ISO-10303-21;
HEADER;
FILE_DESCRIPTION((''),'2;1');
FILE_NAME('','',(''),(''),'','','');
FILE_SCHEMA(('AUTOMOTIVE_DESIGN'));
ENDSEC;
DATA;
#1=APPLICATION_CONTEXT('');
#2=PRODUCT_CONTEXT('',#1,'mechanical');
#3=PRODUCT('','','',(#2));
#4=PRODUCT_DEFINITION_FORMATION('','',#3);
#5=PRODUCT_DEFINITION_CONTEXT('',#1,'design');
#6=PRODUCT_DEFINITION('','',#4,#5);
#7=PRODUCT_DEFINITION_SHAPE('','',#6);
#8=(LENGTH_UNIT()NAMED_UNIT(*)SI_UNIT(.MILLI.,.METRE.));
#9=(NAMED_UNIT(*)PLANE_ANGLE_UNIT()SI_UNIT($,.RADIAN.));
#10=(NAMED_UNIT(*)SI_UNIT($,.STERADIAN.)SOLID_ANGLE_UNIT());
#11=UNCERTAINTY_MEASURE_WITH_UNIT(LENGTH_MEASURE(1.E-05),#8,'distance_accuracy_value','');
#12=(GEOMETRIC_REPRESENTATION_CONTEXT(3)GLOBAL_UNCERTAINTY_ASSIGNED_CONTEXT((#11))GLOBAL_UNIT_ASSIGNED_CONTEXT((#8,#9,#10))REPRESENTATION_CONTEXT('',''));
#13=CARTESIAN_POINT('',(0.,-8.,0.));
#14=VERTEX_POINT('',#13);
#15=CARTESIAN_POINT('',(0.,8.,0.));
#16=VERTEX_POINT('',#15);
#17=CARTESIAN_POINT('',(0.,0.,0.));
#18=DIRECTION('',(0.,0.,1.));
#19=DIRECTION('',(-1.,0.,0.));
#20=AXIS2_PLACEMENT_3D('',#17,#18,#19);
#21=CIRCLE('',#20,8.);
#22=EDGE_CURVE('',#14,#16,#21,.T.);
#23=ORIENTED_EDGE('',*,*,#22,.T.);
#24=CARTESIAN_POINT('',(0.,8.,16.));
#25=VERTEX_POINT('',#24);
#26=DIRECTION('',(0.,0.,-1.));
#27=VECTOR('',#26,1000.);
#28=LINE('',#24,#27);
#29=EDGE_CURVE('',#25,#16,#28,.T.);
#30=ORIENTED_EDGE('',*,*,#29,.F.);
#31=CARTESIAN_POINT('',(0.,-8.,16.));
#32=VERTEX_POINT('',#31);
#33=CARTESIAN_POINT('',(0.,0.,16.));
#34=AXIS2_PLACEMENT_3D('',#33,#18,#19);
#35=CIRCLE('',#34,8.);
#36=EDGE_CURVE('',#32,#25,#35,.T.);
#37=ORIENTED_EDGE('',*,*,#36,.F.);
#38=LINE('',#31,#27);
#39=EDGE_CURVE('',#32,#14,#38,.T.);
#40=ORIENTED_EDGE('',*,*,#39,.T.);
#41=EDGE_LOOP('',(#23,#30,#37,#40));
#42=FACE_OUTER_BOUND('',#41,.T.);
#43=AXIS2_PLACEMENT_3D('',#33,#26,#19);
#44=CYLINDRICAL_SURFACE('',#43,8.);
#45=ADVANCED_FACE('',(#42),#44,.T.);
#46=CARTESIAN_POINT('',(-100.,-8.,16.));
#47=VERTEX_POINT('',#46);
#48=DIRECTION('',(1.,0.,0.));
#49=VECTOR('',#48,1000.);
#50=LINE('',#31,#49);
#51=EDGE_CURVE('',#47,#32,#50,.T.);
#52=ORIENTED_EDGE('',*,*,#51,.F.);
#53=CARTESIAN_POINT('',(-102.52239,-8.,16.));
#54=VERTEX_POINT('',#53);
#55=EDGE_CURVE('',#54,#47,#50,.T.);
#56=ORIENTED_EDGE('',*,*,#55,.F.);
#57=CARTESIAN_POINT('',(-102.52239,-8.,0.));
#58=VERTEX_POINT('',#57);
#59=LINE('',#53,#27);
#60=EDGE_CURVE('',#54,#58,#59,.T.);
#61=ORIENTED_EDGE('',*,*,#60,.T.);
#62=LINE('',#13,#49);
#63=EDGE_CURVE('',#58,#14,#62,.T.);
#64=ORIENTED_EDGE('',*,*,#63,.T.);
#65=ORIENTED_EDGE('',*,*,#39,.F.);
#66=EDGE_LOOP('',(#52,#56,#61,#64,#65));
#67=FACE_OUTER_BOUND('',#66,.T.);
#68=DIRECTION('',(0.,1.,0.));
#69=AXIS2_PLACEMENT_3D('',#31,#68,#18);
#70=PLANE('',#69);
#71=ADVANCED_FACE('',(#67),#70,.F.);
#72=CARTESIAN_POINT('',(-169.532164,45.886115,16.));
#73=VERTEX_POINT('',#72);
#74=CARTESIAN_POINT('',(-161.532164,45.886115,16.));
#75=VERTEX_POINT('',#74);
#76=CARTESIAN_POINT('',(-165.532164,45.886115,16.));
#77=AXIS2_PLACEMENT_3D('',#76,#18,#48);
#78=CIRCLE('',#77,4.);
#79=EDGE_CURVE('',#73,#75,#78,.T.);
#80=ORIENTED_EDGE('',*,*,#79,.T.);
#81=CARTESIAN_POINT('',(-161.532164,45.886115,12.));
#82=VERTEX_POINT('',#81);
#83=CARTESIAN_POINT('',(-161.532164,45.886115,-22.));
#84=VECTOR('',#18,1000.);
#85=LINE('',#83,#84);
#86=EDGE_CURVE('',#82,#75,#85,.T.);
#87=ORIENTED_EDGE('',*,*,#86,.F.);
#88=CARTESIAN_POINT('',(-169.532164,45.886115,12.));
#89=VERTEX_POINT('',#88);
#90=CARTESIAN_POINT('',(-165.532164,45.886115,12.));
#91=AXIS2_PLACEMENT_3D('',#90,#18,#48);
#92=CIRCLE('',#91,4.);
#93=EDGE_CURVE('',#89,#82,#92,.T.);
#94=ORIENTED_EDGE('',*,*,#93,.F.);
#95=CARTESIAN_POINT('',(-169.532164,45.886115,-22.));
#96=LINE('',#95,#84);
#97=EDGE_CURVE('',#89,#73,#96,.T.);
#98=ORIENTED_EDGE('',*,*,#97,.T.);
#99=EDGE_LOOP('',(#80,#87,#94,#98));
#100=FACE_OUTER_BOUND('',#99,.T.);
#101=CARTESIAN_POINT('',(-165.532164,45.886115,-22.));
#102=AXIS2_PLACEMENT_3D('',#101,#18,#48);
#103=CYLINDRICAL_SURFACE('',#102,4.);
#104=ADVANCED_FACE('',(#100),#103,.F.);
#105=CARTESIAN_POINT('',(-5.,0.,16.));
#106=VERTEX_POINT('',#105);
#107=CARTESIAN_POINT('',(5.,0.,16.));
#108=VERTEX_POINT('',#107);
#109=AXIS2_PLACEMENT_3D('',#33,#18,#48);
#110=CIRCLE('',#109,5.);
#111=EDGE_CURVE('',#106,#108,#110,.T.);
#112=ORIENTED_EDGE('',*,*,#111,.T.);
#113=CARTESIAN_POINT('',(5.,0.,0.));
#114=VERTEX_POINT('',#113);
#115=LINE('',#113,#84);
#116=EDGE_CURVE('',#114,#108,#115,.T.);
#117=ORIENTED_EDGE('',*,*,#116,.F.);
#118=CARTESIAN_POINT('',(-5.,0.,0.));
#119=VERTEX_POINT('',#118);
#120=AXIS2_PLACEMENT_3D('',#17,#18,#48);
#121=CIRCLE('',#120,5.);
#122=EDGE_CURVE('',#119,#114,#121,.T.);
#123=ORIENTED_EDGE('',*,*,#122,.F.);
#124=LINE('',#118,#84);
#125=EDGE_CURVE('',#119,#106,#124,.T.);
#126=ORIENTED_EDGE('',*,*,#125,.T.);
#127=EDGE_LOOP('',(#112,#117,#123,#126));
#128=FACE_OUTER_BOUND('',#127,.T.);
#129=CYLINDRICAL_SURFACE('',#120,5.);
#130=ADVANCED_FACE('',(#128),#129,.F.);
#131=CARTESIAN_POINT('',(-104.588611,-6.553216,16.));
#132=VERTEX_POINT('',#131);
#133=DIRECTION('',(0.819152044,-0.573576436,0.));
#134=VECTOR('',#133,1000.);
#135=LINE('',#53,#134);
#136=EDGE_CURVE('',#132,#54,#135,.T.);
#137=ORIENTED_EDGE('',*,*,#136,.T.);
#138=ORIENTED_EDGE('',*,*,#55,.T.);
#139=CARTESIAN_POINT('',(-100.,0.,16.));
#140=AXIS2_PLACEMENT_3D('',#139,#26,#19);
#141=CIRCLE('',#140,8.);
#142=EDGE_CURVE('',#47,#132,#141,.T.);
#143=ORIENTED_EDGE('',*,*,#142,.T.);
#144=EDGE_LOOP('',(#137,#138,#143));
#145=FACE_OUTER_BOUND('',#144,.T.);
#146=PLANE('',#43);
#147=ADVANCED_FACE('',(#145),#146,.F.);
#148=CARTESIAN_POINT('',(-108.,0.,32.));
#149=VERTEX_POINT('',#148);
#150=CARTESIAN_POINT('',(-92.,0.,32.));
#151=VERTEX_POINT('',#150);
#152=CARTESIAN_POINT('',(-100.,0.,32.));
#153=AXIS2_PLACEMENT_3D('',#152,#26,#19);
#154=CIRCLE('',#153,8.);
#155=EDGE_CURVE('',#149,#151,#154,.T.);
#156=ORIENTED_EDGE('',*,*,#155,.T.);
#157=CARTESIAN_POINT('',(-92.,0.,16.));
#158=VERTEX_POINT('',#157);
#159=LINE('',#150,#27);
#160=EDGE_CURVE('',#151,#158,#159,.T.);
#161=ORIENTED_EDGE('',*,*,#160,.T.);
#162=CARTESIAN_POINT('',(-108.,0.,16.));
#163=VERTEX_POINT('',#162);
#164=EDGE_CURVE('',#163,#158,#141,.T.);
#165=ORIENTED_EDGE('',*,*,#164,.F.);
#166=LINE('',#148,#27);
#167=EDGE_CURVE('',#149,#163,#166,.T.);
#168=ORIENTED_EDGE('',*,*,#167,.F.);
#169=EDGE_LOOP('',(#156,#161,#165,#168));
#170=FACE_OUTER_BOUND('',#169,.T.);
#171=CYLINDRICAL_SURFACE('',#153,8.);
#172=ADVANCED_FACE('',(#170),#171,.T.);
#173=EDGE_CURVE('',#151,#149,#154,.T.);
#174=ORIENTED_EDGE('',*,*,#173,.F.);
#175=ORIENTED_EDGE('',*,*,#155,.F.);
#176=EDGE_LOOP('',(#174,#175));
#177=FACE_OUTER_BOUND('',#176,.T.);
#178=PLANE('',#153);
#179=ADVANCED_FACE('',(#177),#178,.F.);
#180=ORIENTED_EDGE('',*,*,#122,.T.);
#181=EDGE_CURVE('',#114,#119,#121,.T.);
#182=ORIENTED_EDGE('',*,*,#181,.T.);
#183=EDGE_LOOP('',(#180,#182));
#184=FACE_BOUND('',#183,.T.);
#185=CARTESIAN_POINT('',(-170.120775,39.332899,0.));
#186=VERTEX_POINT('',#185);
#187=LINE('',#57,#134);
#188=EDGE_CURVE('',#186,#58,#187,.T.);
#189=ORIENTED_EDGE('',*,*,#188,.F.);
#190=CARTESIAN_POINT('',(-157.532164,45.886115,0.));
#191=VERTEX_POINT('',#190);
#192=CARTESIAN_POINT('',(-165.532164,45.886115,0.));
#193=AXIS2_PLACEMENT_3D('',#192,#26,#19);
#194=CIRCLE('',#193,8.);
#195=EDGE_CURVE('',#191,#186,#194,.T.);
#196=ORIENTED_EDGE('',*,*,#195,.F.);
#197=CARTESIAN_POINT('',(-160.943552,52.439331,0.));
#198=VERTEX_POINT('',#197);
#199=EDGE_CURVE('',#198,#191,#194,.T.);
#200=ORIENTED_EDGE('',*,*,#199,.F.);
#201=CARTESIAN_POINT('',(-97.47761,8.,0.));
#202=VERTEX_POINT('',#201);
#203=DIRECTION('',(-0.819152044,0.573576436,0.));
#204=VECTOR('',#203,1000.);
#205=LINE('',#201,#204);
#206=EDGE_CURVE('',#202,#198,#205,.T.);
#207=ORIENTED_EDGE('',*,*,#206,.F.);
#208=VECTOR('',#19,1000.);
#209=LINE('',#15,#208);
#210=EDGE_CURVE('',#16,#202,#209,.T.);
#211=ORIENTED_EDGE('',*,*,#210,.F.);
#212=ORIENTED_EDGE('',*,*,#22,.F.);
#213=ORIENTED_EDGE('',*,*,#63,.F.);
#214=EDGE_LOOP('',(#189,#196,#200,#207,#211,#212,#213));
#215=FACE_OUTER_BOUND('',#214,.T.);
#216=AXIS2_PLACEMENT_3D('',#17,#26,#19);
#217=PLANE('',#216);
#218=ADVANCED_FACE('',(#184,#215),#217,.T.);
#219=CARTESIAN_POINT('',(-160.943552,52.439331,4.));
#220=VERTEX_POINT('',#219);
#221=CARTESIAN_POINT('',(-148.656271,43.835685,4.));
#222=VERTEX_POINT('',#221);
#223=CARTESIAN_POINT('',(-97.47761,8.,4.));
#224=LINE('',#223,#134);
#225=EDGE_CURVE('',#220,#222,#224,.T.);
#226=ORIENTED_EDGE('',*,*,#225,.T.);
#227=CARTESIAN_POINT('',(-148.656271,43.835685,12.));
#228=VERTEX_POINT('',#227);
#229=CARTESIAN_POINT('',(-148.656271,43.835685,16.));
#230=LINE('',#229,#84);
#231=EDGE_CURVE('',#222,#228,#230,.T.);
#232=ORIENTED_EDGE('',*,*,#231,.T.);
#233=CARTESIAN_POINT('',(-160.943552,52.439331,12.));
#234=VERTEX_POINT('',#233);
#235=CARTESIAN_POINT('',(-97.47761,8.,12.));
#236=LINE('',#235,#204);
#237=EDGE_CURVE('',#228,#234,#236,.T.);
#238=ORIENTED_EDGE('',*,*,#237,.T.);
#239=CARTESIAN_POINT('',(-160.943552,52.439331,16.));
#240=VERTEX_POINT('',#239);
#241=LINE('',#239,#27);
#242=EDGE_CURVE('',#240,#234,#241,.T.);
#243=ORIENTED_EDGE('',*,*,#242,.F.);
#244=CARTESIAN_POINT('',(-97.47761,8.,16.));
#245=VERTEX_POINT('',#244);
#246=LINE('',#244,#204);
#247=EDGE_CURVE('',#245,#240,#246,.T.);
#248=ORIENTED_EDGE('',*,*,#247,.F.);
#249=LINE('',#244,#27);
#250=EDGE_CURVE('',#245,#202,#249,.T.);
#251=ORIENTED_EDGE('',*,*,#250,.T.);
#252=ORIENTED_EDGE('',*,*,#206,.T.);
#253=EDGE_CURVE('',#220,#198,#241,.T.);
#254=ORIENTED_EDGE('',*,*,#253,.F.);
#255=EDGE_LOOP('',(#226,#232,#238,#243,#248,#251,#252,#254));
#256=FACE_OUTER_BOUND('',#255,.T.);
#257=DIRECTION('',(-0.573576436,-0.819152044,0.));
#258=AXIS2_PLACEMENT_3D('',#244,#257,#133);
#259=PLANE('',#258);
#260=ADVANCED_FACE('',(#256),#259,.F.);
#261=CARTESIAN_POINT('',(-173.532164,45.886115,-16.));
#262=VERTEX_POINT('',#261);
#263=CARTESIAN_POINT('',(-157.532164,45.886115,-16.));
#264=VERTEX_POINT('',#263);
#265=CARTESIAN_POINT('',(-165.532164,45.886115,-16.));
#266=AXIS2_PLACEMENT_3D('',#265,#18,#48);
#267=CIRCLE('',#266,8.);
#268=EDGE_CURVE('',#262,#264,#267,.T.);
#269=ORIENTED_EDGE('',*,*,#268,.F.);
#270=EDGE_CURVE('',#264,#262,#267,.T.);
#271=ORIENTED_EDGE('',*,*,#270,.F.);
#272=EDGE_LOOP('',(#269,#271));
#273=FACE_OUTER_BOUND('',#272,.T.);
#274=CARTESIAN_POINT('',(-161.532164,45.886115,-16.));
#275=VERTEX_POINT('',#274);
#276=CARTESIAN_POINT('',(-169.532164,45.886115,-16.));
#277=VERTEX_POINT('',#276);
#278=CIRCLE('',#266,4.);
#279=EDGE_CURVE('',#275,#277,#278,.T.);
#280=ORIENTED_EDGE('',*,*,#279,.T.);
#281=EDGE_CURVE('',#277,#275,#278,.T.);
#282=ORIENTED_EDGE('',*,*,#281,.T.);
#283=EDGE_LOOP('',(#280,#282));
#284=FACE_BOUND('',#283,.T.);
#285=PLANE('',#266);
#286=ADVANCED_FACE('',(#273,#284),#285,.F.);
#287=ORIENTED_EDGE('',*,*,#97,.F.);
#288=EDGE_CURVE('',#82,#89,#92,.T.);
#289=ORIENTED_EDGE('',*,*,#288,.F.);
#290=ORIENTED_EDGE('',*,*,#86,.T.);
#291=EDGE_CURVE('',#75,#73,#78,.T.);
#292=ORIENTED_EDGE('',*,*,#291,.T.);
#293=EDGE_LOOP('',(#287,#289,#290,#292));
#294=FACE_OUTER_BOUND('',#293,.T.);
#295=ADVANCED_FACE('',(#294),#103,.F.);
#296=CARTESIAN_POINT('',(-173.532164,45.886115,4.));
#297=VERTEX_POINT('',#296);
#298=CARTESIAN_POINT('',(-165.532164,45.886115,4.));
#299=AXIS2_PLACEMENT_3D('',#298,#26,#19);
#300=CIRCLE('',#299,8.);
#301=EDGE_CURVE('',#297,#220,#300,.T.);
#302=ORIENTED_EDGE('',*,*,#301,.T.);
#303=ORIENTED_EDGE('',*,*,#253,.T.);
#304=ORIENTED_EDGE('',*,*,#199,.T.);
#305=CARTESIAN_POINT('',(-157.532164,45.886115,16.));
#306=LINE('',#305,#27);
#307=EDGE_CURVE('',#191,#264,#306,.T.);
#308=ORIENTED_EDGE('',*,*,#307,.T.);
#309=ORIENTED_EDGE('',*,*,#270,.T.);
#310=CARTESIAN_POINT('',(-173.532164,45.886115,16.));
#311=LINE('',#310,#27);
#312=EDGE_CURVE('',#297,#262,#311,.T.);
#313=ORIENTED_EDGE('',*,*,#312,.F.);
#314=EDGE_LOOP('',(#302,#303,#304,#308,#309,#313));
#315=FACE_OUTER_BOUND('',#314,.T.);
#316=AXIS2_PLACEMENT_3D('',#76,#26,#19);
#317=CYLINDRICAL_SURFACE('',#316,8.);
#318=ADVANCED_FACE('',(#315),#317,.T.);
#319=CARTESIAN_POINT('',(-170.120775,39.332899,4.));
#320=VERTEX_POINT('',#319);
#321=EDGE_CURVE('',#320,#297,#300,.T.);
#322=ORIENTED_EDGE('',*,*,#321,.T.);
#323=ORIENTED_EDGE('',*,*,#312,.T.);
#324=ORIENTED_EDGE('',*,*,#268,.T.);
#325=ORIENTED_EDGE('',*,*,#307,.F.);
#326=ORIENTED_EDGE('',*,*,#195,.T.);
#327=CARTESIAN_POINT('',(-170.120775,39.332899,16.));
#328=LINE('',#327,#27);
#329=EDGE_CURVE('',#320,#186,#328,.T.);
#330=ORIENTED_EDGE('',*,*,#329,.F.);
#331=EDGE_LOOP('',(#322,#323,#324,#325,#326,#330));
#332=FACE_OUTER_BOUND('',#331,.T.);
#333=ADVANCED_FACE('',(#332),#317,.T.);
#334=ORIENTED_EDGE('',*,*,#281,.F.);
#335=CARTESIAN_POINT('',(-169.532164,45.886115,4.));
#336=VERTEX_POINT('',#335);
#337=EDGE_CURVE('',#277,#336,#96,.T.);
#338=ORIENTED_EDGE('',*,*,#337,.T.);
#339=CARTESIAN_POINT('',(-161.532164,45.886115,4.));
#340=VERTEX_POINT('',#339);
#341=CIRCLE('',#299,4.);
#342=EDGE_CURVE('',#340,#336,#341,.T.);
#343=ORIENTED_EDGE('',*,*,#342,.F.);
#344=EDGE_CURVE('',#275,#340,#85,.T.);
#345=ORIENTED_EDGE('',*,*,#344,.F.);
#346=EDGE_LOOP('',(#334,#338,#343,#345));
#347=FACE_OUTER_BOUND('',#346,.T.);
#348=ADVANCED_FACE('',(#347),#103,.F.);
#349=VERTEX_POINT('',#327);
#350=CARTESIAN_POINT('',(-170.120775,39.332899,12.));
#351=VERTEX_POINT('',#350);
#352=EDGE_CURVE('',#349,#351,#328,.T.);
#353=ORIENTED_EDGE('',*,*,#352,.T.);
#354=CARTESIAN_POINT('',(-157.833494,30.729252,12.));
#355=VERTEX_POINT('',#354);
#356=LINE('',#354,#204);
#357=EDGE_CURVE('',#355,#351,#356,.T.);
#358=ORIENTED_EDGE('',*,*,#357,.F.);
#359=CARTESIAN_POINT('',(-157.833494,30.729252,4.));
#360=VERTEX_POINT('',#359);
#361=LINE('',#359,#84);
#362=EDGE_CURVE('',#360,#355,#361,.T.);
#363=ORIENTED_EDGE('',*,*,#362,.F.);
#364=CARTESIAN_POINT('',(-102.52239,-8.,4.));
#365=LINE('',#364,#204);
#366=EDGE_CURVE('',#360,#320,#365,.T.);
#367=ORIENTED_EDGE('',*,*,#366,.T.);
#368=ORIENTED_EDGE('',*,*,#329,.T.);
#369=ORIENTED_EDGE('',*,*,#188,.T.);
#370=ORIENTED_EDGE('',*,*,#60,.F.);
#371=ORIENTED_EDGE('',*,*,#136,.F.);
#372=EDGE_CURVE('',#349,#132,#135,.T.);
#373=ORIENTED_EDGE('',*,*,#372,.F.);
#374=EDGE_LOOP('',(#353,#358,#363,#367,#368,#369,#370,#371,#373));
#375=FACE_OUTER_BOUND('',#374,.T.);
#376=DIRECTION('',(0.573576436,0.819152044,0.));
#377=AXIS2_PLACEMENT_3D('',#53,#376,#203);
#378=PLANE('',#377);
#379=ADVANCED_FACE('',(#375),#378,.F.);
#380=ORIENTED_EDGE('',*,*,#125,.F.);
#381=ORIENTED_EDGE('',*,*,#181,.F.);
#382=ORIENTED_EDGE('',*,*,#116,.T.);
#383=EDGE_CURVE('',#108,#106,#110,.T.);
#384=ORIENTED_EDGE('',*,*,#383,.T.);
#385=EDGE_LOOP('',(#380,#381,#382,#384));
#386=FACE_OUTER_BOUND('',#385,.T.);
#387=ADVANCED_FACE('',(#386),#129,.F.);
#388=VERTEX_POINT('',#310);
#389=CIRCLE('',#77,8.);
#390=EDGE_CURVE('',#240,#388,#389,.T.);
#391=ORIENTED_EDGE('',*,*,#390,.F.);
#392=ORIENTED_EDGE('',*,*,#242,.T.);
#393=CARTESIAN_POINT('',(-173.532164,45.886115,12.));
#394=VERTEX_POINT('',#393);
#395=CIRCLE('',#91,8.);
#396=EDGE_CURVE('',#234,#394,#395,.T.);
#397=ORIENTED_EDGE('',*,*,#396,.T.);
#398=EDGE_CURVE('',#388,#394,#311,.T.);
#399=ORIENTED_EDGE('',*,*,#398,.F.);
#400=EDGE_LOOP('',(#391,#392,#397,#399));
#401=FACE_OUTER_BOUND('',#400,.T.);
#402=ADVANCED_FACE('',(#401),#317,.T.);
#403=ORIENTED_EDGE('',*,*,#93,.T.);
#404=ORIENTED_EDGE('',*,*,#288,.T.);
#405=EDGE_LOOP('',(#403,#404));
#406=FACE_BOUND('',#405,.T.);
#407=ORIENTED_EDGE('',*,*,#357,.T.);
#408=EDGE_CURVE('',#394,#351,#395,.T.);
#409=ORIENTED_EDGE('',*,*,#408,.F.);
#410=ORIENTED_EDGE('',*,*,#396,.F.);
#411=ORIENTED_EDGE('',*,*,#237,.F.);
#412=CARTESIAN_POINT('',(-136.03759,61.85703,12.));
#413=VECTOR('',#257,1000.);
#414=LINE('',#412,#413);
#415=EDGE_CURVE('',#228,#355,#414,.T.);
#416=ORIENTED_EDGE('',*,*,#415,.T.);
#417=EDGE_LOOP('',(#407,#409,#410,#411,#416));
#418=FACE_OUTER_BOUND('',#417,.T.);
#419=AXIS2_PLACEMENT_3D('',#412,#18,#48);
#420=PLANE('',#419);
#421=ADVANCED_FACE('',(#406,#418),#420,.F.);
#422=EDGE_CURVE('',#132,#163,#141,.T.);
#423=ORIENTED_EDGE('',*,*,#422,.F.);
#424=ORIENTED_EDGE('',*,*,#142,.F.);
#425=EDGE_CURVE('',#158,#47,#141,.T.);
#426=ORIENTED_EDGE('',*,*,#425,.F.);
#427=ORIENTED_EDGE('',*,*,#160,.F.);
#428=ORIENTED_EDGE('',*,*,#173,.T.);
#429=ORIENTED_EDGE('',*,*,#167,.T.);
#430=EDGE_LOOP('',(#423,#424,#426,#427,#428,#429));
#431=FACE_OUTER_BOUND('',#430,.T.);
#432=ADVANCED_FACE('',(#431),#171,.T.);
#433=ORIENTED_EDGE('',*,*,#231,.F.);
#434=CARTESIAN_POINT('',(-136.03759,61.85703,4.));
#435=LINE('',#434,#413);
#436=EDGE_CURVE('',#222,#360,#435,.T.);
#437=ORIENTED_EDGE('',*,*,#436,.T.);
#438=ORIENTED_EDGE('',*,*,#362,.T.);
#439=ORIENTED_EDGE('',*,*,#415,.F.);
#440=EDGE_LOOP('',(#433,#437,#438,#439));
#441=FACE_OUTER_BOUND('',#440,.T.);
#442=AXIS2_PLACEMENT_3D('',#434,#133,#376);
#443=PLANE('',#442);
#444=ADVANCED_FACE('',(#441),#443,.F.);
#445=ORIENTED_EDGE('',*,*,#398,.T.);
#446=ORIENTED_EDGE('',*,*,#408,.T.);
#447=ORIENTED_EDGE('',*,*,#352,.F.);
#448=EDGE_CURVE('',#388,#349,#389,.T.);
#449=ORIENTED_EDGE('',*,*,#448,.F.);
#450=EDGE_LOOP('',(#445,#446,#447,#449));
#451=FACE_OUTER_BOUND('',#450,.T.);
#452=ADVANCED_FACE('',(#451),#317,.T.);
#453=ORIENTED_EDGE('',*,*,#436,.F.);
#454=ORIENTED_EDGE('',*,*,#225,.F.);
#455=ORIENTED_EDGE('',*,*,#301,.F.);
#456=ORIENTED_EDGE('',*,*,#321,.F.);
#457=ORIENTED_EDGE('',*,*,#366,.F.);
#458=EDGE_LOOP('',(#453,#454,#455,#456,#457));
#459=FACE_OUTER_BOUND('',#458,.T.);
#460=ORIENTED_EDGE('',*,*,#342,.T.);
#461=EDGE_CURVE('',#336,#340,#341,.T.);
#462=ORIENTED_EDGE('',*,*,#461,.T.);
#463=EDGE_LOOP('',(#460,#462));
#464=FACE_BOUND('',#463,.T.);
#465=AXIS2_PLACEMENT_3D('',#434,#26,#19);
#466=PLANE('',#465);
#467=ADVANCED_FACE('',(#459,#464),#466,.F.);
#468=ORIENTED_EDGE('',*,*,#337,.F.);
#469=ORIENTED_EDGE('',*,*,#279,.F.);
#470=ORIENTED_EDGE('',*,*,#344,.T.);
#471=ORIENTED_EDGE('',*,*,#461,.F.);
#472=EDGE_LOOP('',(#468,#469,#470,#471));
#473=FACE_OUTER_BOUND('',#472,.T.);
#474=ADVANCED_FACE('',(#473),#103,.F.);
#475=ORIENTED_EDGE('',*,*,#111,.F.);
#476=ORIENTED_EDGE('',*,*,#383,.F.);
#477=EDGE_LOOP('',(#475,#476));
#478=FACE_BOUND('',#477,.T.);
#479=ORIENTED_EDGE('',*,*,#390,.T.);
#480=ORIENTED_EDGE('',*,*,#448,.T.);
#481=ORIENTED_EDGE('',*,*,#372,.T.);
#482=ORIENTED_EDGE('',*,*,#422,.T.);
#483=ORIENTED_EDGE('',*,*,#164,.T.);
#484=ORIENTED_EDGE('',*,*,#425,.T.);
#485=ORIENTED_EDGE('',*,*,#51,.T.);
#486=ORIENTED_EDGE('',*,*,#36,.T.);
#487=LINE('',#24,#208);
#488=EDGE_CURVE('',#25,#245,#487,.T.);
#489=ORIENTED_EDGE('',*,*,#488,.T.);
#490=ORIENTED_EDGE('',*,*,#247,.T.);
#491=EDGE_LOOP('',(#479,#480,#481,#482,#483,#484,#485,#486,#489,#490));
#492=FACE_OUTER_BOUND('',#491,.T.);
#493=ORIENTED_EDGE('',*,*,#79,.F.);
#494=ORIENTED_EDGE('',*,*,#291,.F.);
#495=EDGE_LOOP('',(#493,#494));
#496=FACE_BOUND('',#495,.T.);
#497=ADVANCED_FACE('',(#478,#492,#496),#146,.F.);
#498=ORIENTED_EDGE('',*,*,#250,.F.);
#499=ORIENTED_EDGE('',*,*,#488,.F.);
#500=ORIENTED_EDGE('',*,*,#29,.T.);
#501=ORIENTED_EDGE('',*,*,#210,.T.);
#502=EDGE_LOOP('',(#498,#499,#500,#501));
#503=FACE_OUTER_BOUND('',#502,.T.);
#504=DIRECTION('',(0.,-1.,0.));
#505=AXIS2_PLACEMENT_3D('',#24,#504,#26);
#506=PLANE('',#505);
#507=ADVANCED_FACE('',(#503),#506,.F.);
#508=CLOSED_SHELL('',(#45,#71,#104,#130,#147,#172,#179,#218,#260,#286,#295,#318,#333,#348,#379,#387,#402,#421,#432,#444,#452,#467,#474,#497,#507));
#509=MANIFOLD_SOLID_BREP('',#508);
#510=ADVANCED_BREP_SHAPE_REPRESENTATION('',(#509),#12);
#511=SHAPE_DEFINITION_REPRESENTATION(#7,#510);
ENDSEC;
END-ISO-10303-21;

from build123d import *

# Parameters (mm, degrees)
BOSS_EXTRUDE1_DEPTH = 16
SKETCH2_R           = 5
CUT_EXTRUDE1_DEPTH  = 16
SKETCH3_R           = 8
BOSS_EXTRUDE2_DEPTH = 32
BOSS_EXTRUDE3_START = -32
SKETCH4_R           = 8
BOSS_EXTRUDE3_DEPTH = 32
SKETCH5_W           = 30
SKETCH5_H           = 8
CUT_EXTRUDE2_DEPTH  = 38
SKETCH6_R           = 4
CUT_EXTRUDE3_DEPTH  = 38


with BuildPart() as part:
    # Sketch1 → Boss-Extrude1 (new body)
    with BuildSketch(Plane.XY):
        with BuildLine():
            Line((0, 8), (-97.477609689, 8))
            Line((-97.477609689, 8), (-160.943552052, 52.439331262))
            ThreePointArc((-160.943552052, 52.439331262), (-172.085379897, 50.474726399), (-170.120775034, 39.332898554))
            Line((-170.120775034, 39.332898554), (-102.522390311, -8))
            Line((-102.522390311, -8), (0, -8))
            ThreePointArc((0, -8), (8, 0), (0, 8))
        make_face()
    extrude(amount=BOSS_EXTRUDE1_DEPTH)

    # Sketch2 → Cut-Extrude1 (cut)
    with BuildSketch(Plane.XY.offset(16)):
        Circle(SKETCH2_R)
    extrude(amount=-CUT_EXTRUDE1_DEPTH, mode=Mode.SUBTRACT)

    # Sketch3 → Boss-Extrude2 (add)
    with BuildSketch(Plane(origin=(0, 0, 0), x_dir=(-1, 0, 0), z_dir=(0, 0, -1))):
        with Locations((100, 0)):
            Circle(SKETCH3_R)
    extrude(amount=-BOSS_EXTRUDE2_DEPTH)

    # Sketch4 → Boss-Extrude3 (add)
    with BuildSketch(Plane.XY.offset(16).offset(BOSS_EXTRUDE3_START)):
        with Locations(Location((-165.532163543, 45.886114908, 0), (0, 0, 235))):
            Circle(SKETCH4_R)
    extrude(amount=BOSS_EXTRUDE3_DEPTH)

    # Sketch5 → Cut-Extrude2 (cut)
    with BuildSketch(Plane(origin=(-37.487604325, -53.537847394, 0), x_dir=(0.819152044288991, -0.5735764363510472, 0), z_dir=(-0.5735764363510472, -0.819152044288991, 0))):
        with Locations((-161.915204429, 8)):
            Rectangle(SKETCH5_W, SKETCH5_H)
    extrude(amount=-CUT_EXTRUDE2_DEPTH, mode=Mode.SUBTRACT)

    # Sketch6 → Cut-Extrude3 (cut)
    with BuildSketch(Plane.XY.offset(16)):
        with Locations((-165.532163543, 45.886114908)):
            Circle(SKETCH6_R)
    extrude(amount=-CUT_EXTRUDE3_DEPTH, mode=Mode.SUBTRACT)


solid = part.part
